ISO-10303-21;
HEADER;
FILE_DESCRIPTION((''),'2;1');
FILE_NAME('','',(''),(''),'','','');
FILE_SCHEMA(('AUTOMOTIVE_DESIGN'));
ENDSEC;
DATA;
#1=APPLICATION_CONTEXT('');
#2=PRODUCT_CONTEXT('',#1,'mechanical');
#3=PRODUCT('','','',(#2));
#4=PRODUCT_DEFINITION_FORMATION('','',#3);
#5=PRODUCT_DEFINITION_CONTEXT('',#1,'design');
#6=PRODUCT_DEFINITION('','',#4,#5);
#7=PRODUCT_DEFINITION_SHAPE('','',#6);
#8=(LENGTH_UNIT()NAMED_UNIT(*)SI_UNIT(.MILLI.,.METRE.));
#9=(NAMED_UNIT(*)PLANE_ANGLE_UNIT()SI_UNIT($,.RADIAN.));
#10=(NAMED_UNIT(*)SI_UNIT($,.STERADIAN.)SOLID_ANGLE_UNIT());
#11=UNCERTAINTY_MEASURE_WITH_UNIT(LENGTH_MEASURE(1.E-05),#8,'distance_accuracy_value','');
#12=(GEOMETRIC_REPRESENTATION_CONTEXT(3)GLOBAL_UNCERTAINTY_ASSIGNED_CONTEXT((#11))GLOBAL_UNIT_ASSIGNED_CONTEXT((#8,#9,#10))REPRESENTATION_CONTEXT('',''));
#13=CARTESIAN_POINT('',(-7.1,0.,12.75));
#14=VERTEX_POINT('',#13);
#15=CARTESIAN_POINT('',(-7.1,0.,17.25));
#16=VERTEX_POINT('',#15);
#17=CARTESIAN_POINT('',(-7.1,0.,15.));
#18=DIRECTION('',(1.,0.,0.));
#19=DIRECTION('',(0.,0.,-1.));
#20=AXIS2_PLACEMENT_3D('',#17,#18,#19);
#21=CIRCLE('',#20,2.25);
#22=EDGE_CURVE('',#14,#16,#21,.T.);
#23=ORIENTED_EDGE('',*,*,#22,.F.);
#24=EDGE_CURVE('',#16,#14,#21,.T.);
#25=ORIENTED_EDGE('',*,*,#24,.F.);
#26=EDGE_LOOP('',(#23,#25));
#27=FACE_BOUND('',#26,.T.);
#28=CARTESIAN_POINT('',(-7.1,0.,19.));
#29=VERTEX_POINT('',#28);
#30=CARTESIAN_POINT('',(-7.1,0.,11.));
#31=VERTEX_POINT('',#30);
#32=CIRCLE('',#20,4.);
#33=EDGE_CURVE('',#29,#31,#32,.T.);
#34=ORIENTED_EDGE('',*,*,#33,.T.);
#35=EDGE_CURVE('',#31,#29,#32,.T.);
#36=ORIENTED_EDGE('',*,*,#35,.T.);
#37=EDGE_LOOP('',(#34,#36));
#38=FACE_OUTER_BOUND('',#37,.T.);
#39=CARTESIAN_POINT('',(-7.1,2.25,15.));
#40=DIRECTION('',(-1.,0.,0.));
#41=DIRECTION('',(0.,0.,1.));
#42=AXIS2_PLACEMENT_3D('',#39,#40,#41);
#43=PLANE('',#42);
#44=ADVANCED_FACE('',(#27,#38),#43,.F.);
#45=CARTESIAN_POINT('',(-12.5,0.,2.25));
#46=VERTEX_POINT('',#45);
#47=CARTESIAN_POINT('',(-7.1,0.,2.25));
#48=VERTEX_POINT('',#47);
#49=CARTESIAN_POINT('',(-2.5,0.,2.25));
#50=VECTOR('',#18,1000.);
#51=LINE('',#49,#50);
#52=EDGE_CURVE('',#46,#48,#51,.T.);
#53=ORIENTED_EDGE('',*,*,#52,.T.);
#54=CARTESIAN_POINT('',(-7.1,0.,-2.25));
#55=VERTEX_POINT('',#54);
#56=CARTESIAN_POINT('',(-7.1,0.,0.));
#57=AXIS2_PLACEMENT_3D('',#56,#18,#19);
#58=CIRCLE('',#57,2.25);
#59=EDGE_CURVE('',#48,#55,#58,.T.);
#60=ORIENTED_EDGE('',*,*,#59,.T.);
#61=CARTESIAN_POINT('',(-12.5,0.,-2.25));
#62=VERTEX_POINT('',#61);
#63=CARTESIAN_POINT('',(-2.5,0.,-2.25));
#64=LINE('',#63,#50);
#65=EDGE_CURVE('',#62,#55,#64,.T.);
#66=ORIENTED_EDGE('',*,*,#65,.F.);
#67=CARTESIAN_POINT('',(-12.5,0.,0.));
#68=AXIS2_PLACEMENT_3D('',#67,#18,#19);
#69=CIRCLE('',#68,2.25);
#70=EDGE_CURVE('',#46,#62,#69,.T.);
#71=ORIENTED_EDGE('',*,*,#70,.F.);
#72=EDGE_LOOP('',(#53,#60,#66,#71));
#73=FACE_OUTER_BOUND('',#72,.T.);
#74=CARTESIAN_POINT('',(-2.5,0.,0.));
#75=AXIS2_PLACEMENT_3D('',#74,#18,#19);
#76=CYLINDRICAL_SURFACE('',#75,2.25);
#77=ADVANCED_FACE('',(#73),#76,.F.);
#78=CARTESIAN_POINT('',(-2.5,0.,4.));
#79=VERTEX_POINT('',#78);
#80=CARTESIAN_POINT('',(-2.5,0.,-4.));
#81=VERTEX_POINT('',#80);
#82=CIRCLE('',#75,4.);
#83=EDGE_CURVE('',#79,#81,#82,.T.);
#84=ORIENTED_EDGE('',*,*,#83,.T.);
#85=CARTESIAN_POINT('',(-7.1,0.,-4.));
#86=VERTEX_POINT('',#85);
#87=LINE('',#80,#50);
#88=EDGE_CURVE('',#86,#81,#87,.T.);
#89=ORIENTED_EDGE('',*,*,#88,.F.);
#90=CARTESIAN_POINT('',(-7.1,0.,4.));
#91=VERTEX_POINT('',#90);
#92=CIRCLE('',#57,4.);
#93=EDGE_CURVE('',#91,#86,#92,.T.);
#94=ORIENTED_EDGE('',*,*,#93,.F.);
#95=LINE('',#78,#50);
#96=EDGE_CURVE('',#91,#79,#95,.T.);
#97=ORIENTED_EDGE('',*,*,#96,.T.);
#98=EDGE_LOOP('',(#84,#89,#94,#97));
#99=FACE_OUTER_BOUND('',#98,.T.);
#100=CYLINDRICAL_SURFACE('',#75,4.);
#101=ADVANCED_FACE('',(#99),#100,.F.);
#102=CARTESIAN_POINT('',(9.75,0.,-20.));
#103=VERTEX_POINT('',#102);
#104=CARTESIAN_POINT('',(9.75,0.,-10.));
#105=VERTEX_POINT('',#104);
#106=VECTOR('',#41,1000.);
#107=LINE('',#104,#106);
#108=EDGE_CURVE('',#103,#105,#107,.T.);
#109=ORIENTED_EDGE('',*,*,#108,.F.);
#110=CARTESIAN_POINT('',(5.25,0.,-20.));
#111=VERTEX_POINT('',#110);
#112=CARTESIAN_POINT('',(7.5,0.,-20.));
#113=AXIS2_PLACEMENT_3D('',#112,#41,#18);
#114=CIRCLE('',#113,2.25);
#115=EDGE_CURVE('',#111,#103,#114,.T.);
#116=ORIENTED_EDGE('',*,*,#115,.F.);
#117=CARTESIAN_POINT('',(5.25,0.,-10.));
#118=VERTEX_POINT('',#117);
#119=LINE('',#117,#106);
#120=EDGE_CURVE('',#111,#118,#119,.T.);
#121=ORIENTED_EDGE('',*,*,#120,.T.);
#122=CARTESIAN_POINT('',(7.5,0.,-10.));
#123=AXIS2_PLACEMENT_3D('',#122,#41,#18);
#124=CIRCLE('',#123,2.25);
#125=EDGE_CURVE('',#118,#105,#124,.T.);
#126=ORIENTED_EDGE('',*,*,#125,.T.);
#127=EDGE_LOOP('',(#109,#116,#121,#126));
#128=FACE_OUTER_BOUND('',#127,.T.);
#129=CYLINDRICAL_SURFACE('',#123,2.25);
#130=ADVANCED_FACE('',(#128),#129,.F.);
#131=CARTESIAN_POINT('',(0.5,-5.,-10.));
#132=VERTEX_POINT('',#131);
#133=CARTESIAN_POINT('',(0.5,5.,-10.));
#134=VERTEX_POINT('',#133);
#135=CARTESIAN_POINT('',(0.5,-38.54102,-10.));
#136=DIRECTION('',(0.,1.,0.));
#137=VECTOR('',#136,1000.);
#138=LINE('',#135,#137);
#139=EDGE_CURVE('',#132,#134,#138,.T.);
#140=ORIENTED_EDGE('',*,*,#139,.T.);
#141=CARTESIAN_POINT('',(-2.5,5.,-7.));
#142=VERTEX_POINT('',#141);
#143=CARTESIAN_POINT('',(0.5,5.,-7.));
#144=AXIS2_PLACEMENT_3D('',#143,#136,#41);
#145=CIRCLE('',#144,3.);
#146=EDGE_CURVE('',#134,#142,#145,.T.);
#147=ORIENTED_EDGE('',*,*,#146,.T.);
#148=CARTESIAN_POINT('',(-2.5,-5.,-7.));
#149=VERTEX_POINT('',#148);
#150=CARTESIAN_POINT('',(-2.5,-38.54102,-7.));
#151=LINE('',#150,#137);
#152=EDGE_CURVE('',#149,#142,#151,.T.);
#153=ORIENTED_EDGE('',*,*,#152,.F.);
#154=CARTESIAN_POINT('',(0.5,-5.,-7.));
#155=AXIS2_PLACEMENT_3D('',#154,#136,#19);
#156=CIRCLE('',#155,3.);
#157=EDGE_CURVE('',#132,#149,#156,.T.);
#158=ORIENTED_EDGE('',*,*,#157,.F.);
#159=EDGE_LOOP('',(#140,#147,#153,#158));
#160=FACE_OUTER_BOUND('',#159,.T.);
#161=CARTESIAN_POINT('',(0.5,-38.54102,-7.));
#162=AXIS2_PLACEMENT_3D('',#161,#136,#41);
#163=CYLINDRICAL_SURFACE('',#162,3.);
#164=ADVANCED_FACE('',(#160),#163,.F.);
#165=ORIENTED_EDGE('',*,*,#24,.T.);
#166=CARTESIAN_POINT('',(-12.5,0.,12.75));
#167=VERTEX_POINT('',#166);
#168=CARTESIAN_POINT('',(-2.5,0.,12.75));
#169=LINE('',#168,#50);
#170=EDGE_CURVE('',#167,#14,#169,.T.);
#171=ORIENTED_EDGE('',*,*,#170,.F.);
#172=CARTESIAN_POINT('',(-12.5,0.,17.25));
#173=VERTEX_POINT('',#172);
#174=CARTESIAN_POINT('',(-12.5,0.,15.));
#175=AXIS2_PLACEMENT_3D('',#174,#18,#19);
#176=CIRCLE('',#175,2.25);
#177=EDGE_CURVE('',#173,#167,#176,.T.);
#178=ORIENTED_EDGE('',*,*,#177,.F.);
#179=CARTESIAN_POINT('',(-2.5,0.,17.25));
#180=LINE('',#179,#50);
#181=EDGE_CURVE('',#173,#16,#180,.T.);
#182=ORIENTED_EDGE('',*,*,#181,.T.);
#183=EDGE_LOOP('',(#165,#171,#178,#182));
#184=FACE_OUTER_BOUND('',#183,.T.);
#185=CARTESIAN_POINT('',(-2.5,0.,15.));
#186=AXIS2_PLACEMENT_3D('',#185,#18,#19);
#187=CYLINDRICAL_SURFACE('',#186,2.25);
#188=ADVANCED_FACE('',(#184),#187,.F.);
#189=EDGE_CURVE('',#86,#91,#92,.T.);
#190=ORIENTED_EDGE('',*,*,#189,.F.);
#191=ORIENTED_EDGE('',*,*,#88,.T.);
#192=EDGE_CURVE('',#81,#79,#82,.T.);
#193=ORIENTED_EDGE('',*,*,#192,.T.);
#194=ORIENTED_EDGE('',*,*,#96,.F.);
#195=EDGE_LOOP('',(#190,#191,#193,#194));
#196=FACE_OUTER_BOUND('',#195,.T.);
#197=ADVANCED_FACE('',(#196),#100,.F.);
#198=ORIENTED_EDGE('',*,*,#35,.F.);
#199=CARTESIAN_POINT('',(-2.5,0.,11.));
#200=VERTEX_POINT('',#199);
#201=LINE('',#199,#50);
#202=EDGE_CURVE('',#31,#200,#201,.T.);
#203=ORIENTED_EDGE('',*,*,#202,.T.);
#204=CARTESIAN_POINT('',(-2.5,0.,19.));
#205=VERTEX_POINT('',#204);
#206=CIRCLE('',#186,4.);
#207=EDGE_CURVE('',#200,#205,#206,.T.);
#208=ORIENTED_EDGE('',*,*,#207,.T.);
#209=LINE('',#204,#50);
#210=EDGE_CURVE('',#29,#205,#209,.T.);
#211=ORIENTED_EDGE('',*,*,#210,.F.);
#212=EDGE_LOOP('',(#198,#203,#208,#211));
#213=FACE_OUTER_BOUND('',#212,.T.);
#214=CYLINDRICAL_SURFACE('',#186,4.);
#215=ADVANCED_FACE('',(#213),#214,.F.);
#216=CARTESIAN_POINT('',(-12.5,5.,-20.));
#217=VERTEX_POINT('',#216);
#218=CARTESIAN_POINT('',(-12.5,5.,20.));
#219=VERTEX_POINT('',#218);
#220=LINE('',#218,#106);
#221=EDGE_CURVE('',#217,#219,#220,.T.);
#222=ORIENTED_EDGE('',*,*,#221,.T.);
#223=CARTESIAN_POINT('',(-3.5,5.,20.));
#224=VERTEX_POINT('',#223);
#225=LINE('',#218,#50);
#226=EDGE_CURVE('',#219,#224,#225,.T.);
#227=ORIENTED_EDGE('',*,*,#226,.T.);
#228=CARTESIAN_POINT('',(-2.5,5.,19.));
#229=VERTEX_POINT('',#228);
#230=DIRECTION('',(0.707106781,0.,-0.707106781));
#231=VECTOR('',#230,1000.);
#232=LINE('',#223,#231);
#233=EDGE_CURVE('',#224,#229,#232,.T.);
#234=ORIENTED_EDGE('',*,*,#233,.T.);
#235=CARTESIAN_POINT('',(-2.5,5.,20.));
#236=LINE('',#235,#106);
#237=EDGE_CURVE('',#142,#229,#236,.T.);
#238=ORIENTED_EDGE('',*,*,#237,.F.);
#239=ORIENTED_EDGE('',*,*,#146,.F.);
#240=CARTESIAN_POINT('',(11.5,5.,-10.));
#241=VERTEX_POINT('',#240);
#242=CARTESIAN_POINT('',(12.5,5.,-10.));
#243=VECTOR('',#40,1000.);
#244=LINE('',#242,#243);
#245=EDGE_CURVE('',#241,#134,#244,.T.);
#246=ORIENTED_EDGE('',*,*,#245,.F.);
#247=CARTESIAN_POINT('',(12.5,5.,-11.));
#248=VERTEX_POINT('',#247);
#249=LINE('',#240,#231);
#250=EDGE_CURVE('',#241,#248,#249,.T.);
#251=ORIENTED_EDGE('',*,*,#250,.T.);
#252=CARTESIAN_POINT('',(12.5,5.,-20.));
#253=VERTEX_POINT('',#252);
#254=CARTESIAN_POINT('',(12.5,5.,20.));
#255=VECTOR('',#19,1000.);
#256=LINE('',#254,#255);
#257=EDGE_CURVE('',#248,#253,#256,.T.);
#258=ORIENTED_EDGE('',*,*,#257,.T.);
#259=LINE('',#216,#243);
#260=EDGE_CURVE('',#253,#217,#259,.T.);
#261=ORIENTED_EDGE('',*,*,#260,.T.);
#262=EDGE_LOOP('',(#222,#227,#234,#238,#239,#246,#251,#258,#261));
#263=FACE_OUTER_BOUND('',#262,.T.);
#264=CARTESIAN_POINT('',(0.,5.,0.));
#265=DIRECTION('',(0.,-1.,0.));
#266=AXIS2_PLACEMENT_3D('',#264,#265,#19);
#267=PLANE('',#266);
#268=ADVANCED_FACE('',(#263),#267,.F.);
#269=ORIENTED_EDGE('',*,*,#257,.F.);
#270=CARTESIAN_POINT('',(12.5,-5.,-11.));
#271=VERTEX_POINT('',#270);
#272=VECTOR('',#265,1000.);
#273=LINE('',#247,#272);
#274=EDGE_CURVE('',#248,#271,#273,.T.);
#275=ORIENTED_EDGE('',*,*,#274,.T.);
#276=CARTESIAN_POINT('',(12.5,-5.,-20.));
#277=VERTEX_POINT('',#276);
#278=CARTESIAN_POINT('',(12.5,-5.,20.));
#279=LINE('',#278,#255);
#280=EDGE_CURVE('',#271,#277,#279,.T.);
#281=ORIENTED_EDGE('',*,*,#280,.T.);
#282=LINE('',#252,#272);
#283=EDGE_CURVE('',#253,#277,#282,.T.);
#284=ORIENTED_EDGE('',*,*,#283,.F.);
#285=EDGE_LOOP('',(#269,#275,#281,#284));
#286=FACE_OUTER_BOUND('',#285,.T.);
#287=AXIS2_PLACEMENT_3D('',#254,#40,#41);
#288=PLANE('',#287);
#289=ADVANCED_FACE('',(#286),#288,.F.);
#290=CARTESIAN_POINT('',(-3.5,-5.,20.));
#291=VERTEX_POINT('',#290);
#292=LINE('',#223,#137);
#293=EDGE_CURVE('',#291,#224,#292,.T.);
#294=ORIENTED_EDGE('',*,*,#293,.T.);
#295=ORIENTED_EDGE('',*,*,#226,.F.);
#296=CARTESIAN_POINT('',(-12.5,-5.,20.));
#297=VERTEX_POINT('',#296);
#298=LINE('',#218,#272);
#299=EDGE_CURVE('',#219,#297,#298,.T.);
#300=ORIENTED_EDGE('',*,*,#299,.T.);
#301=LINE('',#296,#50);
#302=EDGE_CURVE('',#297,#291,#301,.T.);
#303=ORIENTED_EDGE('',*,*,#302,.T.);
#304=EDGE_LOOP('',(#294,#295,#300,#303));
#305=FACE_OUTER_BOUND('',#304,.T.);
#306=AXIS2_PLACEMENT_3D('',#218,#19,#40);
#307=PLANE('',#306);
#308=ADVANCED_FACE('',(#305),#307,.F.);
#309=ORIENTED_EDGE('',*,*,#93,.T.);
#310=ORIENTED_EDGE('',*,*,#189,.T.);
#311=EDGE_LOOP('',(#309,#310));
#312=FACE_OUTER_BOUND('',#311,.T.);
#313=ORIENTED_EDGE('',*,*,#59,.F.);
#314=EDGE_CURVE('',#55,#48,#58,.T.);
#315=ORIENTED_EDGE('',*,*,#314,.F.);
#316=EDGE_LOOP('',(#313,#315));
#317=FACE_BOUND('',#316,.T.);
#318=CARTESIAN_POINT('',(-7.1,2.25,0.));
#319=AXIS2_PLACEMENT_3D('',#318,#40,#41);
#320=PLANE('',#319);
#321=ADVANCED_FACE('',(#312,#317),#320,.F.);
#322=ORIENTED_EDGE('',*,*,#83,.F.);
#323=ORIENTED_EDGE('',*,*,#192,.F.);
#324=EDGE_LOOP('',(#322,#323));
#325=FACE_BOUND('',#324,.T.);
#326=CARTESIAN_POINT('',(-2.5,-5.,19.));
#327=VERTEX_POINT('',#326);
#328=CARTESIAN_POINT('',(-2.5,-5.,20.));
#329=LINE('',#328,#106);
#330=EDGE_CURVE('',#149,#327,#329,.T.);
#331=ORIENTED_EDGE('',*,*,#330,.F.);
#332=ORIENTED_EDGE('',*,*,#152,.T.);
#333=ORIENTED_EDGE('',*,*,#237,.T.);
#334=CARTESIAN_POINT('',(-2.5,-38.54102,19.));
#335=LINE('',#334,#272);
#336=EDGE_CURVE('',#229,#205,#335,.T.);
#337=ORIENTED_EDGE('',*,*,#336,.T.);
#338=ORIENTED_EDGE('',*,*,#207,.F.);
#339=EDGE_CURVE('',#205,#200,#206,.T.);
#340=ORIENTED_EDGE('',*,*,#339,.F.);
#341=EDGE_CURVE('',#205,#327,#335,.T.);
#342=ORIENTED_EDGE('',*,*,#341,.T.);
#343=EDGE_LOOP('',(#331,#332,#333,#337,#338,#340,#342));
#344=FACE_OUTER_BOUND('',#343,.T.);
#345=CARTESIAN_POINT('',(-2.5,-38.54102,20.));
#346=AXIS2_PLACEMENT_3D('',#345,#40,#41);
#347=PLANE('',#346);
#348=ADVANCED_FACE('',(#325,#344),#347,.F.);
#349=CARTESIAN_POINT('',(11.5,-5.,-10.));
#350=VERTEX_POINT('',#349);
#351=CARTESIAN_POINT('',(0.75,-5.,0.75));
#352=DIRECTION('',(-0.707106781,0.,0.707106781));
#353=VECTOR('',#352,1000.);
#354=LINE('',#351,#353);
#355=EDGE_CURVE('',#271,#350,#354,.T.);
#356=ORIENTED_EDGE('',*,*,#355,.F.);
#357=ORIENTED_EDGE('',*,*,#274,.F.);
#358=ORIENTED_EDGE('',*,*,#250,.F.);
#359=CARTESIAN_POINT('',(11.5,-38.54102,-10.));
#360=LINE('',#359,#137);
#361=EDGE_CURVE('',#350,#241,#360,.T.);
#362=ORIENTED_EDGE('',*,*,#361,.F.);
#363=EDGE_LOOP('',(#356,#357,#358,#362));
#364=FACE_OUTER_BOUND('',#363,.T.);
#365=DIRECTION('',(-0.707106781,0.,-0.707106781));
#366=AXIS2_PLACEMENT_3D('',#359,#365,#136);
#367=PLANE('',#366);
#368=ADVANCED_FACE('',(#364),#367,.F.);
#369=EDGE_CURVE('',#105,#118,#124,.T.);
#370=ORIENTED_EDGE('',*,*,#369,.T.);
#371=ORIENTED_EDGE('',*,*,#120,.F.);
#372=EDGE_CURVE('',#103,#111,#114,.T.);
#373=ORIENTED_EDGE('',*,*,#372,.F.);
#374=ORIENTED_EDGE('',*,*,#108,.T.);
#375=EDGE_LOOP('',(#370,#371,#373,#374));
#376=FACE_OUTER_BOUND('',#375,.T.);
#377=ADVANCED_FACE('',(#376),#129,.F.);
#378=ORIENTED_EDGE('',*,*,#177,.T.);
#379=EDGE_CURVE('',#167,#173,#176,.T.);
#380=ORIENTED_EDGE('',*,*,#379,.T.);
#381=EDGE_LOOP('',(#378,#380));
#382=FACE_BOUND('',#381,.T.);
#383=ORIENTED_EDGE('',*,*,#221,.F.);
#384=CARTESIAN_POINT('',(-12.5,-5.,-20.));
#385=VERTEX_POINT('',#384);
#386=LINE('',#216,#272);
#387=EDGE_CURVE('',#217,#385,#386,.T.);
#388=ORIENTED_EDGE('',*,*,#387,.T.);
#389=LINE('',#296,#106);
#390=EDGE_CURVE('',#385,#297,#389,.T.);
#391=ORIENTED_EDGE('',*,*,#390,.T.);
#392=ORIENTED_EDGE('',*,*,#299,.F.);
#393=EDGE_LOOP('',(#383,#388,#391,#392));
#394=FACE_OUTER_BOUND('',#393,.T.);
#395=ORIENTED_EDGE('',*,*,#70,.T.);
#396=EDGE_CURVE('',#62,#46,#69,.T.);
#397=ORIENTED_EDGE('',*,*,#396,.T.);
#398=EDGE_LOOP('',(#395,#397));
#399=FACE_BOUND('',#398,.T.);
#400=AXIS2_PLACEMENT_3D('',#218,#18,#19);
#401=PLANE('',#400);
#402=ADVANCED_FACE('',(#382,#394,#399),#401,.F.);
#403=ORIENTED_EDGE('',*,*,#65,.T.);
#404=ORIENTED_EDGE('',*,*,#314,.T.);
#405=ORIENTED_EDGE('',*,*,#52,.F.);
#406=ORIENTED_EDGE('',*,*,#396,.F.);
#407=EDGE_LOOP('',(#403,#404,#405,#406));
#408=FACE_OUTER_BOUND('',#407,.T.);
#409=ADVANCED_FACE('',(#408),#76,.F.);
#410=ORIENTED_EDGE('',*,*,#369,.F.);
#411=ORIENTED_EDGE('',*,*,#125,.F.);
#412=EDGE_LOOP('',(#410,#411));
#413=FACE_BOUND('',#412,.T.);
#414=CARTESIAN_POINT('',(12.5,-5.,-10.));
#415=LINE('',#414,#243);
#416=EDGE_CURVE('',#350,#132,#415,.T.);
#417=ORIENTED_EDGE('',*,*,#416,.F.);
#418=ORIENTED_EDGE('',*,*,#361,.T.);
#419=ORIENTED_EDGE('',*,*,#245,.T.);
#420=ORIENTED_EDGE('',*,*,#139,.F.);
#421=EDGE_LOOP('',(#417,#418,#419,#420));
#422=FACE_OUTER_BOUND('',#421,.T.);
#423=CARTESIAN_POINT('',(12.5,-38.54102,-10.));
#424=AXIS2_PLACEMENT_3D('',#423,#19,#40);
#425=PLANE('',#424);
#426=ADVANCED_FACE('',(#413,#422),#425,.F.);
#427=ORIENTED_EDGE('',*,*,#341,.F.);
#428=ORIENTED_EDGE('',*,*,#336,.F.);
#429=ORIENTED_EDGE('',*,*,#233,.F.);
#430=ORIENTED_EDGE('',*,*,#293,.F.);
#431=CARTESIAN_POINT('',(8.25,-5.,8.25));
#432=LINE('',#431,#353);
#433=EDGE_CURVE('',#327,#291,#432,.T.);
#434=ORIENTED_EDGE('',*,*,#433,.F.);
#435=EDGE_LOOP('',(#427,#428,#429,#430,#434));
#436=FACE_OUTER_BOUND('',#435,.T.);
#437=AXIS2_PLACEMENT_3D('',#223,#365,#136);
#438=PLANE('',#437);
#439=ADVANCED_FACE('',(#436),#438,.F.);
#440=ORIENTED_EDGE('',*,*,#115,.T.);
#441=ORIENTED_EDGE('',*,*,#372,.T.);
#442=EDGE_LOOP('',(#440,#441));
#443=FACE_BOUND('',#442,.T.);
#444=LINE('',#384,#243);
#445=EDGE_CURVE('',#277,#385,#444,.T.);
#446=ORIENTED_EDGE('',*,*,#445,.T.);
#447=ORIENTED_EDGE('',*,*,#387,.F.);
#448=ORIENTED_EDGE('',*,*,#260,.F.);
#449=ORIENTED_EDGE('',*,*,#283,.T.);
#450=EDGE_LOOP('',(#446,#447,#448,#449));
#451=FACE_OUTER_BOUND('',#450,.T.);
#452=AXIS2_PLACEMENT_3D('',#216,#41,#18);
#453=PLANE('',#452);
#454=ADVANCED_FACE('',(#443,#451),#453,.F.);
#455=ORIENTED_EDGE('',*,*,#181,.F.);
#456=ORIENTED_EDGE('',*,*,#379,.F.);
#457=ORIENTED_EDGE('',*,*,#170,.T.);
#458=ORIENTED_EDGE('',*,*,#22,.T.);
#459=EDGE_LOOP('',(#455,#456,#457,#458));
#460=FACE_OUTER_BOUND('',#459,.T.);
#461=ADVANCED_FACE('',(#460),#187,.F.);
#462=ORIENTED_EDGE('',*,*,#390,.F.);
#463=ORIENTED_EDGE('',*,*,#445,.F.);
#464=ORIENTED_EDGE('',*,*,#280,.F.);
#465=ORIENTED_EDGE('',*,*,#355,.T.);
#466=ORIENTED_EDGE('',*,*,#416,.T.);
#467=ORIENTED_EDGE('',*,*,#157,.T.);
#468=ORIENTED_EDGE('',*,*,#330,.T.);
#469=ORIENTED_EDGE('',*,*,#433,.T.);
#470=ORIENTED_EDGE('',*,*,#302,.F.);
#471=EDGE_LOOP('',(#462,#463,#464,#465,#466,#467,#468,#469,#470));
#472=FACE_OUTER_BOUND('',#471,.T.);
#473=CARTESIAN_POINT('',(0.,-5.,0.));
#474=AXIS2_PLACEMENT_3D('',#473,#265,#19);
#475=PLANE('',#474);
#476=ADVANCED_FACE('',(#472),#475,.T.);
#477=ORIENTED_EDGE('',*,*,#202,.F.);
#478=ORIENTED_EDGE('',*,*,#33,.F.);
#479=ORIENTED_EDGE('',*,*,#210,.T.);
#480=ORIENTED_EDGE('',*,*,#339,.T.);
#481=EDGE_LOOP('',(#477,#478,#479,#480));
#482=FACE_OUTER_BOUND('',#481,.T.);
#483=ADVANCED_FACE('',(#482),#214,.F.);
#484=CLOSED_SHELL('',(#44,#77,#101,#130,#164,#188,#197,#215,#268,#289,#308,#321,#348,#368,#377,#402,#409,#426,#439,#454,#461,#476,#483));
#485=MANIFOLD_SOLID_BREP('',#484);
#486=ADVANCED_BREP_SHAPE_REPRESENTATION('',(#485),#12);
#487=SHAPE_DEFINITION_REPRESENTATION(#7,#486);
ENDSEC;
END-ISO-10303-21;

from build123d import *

# Parameters (mm, degrees)
SKETCH_1_W                = 25
SKETCH_1_H                = 40
EXTRUDE_1_DEPTH           = 5
CUT_EXTRUDE_1_DEPTH       = 10
CHAMFER_1_SIZE            = 1
HOLE_WIZARD_1_D           = 4.5
HOLE_WIZARD_1_CBORE_D     = 8
HOLE_WIZARD_1_CBORE_DEPTH = 4.6
HOLE_WIZARD_M4_1_D        = 4.5


with BuildPart() as part:
    # 草图1 → 凸台-拉伸1 (new, symmetric)
    with BuildSketch(Plane(origin=(0, 0, 0), x_dir=(1, 0, 0), z_dir=(0, 1, 0))):
        Rectangle(SKETCH_1_W, SKETCH_1_H)
    extrude(amount=EXTRUDE_1_DEPTH, both=True)

    # 草图2 → 切除-拉伸1 (cut)
    with BuildSketch(Plane(origin=(0, 5, 0), x_dir=(1, 0, 0), z_dir=(0, 1, 0))):
        with BuildLine():
            Line((12.5, -20), (-2.5, -20))
            Line((-2.5, -20), (-2.5, 7))
            ThreePointArc((-2.5, 7), (-1.621320344, 9.121320344), (0.5, 10))
            Line((0.5, 10), (12.5, 10))
            Line((12.5, 10), (12.5, -20))
        make_face()
    extrude(amount=-CUT_EXTRUDE_1_DEPTH, mode=Mode.SUBTRACT)

    # 倒角1
    chamfer_1_edges = [part.edges().sort_by_distance(p)[0] for p in [
        (-2.5, 0, 20),
        (12.5, 0, -10),
    ]]
    chamfer(chamfer_1_edges, length=CHAMFER_1_SIZE)

    # 打孔尺寸(%根据)内六角圆柱头螺钉的类型1 (through all)
    with Locations(Plane(origin=(-2.5, 0, 0), x_dir=(0, 0, -1), z_dir=(1, 0, 0))):
        with Locations((-15, 0), (0, 0)):
            CounterBoreHole(HOLE_WIZARD_1_D / 2, HOLE_WIZARD_1_CBORE_D / 2, HOLE_WIZARD_1_CBORE_DEPTH)

    # M4 间隙孔1 (through all)
    with Locations(Plane.XY.offset(-10)):
        with Locations((7.5, 0)):
            Hole(HOLE_WIZARD_M4_1_D / 2)


solid = part.part
